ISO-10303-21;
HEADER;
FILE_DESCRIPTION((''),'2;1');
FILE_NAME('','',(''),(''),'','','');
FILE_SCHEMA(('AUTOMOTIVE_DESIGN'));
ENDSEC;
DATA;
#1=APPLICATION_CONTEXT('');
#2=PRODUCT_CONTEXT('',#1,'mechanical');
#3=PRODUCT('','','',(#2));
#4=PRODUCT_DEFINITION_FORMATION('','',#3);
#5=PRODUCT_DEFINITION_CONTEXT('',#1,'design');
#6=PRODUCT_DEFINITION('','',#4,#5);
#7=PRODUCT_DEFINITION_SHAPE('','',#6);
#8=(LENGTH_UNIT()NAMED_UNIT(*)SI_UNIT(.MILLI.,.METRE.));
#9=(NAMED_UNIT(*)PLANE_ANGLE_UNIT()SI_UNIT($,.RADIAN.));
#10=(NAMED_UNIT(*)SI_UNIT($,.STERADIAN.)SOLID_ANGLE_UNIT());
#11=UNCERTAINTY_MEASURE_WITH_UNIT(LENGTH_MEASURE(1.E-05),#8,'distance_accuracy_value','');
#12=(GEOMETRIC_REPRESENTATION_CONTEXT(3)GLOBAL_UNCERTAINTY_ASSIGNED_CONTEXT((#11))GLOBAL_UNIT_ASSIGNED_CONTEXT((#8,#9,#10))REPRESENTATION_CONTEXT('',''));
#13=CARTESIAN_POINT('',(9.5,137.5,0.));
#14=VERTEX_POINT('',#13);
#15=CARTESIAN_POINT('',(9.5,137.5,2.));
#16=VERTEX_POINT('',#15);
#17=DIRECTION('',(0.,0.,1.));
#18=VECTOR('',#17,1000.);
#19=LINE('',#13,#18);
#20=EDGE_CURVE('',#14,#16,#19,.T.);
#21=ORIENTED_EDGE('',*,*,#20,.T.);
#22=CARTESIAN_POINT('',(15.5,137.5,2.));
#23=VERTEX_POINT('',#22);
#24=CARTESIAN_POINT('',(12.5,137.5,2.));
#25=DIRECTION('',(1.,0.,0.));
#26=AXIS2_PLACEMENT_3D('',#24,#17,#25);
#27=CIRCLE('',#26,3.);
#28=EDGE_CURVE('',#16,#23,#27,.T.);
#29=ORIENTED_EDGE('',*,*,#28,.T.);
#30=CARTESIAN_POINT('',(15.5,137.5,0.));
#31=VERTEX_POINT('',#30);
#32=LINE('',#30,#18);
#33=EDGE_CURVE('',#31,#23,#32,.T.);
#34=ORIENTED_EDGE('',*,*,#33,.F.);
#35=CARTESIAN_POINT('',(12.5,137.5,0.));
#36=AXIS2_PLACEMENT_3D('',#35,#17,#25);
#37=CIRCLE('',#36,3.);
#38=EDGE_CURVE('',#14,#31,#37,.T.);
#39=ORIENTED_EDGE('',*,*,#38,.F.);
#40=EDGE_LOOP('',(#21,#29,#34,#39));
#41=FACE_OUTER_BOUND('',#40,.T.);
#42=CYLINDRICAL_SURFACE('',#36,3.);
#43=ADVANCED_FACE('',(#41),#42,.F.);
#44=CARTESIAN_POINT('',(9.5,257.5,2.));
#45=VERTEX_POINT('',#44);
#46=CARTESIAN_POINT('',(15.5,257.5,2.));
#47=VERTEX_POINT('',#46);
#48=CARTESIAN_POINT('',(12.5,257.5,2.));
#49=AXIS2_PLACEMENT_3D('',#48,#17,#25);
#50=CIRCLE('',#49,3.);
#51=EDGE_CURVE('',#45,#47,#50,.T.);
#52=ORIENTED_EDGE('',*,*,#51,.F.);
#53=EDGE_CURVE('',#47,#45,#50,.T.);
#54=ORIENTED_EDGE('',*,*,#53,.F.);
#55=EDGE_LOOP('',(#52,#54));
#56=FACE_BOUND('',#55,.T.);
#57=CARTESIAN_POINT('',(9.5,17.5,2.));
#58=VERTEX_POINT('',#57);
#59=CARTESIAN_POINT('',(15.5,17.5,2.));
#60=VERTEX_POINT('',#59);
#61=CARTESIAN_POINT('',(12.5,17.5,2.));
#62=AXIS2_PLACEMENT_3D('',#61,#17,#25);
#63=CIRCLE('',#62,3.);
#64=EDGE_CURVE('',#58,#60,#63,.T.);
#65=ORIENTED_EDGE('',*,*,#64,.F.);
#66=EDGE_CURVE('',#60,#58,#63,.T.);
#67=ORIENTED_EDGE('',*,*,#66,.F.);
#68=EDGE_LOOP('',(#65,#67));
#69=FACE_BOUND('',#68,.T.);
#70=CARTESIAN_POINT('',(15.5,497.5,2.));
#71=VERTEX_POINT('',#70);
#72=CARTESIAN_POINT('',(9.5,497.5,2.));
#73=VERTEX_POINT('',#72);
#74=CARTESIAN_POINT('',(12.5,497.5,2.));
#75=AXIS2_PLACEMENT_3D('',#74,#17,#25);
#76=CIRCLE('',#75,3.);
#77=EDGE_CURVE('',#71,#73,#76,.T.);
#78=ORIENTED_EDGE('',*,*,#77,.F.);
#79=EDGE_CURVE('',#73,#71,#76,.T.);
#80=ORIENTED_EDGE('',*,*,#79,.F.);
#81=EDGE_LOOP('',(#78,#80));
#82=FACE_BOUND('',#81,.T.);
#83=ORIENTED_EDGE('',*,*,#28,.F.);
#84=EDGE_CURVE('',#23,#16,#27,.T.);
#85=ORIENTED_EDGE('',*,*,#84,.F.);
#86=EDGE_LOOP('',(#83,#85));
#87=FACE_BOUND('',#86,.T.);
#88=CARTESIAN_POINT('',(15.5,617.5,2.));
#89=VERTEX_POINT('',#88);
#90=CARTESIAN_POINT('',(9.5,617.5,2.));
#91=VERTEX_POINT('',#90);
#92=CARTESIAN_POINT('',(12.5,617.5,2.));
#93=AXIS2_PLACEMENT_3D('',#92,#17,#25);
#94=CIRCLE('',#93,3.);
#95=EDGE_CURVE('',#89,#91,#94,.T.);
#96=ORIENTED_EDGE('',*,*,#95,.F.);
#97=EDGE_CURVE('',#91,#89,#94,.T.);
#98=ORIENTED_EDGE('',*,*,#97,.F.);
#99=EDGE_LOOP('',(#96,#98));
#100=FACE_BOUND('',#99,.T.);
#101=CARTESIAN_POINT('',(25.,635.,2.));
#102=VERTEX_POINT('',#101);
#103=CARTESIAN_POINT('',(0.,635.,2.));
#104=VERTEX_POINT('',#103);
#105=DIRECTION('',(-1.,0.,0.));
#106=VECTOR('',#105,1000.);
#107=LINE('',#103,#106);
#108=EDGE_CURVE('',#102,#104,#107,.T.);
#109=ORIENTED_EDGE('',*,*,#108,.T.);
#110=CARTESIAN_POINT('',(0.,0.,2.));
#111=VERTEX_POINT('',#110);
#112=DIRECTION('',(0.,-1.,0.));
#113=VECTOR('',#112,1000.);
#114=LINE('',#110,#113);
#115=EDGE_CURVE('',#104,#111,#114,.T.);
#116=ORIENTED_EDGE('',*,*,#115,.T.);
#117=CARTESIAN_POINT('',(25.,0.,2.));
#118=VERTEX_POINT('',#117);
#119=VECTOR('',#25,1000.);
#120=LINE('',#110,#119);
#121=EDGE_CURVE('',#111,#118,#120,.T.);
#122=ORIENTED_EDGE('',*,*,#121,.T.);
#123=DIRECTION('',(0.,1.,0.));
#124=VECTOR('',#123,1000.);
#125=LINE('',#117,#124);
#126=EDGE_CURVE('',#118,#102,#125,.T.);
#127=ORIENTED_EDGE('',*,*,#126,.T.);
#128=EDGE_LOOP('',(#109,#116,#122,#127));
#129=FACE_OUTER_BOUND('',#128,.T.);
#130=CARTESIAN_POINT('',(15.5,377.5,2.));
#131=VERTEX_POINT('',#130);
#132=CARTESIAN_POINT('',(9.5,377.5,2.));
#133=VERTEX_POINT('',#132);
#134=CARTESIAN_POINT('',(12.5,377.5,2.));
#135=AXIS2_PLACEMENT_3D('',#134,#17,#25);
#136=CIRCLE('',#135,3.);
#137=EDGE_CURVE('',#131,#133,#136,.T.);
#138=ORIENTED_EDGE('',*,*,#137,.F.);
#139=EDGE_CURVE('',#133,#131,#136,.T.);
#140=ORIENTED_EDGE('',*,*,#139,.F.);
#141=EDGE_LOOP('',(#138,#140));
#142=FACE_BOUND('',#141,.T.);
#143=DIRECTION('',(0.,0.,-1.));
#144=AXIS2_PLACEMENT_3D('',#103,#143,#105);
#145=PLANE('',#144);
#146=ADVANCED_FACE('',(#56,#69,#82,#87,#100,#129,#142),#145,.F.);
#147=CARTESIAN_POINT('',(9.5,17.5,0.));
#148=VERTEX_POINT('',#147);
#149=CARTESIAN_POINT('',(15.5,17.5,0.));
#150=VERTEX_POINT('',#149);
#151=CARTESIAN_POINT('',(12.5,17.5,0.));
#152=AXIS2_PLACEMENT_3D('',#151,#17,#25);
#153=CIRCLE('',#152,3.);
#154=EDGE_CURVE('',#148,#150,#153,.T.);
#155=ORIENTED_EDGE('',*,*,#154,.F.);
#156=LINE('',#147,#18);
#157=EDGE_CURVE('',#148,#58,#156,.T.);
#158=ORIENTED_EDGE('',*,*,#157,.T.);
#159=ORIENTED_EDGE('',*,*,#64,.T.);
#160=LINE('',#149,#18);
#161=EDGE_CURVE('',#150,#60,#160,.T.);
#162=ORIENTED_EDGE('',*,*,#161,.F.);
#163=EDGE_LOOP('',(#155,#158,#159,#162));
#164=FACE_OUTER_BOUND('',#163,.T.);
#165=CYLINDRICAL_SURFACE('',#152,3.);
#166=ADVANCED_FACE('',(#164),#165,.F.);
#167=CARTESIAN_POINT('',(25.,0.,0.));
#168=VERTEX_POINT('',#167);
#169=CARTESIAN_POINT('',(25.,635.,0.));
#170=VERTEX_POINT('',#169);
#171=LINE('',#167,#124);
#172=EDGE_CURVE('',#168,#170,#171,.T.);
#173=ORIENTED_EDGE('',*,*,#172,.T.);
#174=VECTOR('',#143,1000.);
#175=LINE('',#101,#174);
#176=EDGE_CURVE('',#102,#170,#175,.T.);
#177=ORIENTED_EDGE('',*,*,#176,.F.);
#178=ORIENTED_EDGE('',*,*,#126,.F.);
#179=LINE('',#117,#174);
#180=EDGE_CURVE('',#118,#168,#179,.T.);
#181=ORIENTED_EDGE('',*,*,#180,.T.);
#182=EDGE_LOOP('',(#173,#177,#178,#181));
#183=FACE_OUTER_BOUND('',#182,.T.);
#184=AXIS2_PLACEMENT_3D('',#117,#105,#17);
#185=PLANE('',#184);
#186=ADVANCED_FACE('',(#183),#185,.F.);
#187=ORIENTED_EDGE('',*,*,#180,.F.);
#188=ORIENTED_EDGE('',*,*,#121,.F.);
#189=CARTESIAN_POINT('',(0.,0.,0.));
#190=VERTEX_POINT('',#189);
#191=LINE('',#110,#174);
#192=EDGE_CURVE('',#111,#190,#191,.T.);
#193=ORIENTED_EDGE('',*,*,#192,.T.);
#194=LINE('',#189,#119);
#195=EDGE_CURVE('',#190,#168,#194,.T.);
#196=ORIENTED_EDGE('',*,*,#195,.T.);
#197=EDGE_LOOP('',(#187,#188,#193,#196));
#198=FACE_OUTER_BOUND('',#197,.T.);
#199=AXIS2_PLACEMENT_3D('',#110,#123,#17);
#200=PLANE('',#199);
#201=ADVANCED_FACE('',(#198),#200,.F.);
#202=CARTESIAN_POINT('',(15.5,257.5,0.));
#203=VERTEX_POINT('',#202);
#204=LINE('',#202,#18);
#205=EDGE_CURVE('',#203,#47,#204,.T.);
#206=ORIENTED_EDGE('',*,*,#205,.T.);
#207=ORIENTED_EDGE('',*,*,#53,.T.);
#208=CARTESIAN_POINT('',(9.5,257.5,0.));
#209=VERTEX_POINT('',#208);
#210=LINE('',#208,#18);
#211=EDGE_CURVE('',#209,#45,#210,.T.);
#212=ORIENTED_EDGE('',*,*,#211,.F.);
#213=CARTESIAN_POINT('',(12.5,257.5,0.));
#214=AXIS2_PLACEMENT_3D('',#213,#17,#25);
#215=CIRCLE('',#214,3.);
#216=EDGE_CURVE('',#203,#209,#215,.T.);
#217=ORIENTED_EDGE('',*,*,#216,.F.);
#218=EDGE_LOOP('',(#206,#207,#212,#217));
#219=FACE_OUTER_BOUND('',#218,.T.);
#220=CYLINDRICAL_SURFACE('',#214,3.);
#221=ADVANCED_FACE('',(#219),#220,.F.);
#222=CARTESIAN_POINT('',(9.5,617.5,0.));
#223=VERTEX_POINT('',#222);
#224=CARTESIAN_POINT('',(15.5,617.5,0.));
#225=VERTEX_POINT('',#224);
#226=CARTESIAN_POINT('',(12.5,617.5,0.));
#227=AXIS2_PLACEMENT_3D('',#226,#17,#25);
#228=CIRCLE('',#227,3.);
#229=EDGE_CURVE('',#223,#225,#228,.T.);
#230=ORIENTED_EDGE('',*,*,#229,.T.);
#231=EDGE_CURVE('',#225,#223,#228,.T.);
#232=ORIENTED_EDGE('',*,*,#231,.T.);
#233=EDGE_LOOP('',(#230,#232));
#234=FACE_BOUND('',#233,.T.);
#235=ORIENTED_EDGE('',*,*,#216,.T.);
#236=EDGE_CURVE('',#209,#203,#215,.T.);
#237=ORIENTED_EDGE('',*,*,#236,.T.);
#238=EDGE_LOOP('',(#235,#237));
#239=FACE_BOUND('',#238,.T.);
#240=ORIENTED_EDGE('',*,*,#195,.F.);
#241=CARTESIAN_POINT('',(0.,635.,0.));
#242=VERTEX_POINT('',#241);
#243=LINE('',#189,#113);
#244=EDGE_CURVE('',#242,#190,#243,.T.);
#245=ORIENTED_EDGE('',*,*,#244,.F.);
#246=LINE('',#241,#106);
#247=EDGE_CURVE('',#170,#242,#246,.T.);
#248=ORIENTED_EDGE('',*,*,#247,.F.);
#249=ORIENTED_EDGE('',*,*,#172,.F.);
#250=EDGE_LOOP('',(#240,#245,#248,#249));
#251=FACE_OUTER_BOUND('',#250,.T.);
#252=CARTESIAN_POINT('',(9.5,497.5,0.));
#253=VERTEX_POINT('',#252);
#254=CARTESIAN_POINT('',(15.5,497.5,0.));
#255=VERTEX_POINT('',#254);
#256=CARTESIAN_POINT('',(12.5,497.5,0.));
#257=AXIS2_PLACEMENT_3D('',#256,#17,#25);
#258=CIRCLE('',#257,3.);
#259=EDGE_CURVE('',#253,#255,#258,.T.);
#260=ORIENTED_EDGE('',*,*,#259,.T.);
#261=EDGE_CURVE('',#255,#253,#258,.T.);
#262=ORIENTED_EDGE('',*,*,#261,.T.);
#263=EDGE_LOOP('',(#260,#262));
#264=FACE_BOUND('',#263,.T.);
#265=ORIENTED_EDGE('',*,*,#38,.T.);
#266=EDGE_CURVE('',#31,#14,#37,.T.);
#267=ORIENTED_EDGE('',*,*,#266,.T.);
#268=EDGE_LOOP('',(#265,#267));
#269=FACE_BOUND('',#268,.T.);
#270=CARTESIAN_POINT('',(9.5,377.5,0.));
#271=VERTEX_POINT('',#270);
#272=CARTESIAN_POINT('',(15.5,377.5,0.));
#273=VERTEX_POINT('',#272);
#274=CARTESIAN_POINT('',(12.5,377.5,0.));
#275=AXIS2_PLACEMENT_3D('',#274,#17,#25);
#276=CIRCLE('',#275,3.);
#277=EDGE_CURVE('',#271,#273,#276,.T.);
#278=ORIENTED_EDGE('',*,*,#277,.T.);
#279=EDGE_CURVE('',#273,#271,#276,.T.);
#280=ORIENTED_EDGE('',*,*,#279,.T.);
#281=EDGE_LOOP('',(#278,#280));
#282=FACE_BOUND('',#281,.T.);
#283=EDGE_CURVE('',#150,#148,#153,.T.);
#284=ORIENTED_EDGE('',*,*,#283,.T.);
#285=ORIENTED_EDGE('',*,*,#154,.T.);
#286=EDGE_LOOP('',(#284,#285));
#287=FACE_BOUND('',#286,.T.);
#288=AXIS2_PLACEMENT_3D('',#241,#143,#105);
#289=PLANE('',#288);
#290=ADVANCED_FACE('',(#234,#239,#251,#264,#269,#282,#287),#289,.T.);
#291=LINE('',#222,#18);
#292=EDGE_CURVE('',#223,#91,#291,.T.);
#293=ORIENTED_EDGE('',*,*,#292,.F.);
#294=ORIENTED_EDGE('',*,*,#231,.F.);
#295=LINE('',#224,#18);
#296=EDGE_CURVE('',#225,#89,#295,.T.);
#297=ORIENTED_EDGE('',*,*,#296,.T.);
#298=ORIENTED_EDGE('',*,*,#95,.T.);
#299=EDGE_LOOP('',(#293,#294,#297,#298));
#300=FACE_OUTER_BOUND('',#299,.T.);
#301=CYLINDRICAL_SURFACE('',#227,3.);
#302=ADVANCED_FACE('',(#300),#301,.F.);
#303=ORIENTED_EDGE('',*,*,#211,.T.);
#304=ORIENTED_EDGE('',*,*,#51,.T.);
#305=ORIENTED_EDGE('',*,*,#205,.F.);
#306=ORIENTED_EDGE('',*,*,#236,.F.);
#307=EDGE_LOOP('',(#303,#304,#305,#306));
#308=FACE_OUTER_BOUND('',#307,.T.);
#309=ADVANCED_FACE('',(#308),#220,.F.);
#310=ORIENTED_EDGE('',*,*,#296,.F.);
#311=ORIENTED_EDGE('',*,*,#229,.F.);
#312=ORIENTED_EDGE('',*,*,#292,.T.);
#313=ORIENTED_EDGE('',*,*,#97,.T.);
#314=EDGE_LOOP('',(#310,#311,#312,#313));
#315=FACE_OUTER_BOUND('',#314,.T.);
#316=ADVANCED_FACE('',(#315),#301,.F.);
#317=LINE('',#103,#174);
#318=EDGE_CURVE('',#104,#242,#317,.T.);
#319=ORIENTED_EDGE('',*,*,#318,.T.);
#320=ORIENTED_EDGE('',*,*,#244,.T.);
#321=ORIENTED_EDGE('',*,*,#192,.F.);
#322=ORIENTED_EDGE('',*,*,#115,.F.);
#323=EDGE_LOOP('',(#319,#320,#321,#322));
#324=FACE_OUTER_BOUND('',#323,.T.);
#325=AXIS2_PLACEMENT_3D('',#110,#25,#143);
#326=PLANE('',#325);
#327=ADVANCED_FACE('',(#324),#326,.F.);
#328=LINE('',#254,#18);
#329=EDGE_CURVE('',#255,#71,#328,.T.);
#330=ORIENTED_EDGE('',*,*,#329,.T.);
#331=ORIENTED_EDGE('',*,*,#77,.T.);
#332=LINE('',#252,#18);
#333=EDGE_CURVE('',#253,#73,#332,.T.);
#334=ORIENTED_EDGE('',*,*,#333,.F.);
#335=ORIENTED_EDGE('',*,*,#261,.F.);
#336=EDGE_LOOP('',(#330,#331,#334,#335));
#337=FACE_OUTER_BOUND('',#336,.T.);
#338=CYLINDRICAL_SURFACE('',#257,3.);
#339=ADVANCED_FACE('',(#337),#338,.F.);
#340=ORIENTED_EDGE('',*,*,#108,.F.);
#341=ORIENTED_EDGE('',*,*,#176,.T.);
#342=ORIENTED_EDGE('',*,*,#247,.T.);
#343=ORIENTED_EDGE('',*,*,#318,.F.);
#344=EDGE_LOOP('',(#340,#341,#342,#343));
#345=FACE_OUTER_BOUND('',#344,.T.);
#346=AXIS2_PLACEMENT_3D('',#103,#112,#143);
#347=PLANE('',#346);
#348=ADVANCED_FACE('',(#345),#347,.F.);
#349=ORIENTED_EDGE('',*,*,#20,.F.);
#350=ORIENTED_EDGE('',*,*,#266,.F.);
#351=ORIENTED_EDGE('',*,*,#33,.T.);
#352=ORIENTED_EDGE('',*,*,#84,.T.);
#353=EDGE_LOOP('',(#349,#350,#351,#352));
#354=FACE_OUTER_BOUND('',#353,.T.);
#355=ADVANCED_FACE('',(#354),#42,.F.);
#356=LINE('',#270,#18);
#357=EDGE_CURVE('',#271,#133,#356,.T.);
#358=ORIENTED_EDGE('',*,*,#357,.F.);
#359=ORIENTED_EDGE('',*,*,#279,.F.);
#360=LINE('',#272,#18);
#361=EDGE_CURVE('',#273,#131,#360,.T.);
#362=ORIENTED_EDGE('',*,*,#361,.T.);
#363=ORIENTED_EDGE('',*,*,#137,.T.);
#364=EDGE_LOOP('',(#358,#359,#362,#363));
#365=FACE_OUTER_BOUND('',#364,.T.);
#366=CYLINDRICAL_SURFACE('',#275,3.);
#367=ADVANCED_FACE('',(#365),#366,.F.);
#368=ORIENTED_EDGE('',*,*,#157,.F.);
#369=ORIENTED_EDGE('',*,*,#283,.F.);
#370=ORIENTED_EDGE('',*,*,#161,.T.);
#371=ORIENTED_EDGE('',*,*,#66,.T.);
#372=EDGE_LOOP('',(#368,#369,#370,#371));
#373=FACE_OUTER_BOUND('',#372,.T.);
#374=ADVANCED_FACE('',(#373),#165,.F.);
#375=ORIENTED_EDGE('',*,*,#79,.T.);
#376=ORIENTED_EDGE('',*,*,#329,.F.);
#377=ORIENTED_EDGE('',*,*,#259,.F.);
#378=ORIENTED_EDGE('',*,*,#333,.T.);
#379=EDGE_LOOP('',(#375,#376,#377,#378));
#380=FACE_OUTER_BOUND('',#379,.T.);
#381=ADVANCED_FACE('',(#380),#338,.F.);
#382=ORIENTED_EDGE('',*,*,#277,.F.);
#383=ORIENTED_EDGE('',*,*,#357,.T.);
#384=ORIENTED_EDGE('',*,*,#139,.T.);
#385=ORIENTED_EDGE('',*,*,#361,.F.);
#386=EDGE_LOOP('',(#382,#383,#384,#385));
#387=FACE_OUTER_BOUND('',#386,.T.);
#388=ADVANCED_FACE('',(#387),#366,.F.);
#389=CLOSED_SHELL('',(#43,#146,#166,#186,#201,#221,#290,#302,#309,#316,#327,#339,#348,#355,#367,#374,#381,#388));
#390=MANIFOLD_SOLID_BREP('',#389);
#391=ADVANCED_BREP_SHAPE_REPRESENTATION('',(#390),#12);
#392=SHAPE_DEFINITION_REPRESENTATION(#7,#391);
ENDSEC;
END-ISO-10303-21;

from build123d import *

# Parameters (mm, degrees)
SKETCH_1_W             = 25
SKETCH_1_H             = 635
EXTRUDE_1_DEPTH        = 2
SKETCH_3_R             = 3
CUT_EXTRUDE_1_DEPTH    = 636.495082593
PATTERN_LINEAR_1_COUNT = 6
PATTERN_LINEAR_1_PITCH = 120


with BuildPart() as part:
    # 草图1 → 拉伸1 (new body)
    with BuildSketch(Plane.XY):
        with Locations((12.5, 317.5)):
            Rectangle(SKETCH_1_W, SKETCH_1_H)
    extrude(amount=EXTRUDE_1_DEPTH)

    # 草图3 → 切除-拉伸1 (cut, through all)
    with BuildSketch(Plane.XY.offset(2)):
        with Locations((12.5, 617.5)):
            Circle(SKETCH_3_R)
    cut_extrude_1 = extrude(amount=-CUT_EXTRUDE_1_DEPTH, mode=Mode.SUBTRACT)

    # 阵列(线性)1: 切除-拉伸1 ×6
    with Locations(*[(0, -i * PATTERN_LINEAR_1_PITCH, 0) for i in range(1, PATTERN_LINEAR_1_COUNT)]):
        add(cut_extrude_1, mode=Mode.SUBTRACT)


solid = part.part
